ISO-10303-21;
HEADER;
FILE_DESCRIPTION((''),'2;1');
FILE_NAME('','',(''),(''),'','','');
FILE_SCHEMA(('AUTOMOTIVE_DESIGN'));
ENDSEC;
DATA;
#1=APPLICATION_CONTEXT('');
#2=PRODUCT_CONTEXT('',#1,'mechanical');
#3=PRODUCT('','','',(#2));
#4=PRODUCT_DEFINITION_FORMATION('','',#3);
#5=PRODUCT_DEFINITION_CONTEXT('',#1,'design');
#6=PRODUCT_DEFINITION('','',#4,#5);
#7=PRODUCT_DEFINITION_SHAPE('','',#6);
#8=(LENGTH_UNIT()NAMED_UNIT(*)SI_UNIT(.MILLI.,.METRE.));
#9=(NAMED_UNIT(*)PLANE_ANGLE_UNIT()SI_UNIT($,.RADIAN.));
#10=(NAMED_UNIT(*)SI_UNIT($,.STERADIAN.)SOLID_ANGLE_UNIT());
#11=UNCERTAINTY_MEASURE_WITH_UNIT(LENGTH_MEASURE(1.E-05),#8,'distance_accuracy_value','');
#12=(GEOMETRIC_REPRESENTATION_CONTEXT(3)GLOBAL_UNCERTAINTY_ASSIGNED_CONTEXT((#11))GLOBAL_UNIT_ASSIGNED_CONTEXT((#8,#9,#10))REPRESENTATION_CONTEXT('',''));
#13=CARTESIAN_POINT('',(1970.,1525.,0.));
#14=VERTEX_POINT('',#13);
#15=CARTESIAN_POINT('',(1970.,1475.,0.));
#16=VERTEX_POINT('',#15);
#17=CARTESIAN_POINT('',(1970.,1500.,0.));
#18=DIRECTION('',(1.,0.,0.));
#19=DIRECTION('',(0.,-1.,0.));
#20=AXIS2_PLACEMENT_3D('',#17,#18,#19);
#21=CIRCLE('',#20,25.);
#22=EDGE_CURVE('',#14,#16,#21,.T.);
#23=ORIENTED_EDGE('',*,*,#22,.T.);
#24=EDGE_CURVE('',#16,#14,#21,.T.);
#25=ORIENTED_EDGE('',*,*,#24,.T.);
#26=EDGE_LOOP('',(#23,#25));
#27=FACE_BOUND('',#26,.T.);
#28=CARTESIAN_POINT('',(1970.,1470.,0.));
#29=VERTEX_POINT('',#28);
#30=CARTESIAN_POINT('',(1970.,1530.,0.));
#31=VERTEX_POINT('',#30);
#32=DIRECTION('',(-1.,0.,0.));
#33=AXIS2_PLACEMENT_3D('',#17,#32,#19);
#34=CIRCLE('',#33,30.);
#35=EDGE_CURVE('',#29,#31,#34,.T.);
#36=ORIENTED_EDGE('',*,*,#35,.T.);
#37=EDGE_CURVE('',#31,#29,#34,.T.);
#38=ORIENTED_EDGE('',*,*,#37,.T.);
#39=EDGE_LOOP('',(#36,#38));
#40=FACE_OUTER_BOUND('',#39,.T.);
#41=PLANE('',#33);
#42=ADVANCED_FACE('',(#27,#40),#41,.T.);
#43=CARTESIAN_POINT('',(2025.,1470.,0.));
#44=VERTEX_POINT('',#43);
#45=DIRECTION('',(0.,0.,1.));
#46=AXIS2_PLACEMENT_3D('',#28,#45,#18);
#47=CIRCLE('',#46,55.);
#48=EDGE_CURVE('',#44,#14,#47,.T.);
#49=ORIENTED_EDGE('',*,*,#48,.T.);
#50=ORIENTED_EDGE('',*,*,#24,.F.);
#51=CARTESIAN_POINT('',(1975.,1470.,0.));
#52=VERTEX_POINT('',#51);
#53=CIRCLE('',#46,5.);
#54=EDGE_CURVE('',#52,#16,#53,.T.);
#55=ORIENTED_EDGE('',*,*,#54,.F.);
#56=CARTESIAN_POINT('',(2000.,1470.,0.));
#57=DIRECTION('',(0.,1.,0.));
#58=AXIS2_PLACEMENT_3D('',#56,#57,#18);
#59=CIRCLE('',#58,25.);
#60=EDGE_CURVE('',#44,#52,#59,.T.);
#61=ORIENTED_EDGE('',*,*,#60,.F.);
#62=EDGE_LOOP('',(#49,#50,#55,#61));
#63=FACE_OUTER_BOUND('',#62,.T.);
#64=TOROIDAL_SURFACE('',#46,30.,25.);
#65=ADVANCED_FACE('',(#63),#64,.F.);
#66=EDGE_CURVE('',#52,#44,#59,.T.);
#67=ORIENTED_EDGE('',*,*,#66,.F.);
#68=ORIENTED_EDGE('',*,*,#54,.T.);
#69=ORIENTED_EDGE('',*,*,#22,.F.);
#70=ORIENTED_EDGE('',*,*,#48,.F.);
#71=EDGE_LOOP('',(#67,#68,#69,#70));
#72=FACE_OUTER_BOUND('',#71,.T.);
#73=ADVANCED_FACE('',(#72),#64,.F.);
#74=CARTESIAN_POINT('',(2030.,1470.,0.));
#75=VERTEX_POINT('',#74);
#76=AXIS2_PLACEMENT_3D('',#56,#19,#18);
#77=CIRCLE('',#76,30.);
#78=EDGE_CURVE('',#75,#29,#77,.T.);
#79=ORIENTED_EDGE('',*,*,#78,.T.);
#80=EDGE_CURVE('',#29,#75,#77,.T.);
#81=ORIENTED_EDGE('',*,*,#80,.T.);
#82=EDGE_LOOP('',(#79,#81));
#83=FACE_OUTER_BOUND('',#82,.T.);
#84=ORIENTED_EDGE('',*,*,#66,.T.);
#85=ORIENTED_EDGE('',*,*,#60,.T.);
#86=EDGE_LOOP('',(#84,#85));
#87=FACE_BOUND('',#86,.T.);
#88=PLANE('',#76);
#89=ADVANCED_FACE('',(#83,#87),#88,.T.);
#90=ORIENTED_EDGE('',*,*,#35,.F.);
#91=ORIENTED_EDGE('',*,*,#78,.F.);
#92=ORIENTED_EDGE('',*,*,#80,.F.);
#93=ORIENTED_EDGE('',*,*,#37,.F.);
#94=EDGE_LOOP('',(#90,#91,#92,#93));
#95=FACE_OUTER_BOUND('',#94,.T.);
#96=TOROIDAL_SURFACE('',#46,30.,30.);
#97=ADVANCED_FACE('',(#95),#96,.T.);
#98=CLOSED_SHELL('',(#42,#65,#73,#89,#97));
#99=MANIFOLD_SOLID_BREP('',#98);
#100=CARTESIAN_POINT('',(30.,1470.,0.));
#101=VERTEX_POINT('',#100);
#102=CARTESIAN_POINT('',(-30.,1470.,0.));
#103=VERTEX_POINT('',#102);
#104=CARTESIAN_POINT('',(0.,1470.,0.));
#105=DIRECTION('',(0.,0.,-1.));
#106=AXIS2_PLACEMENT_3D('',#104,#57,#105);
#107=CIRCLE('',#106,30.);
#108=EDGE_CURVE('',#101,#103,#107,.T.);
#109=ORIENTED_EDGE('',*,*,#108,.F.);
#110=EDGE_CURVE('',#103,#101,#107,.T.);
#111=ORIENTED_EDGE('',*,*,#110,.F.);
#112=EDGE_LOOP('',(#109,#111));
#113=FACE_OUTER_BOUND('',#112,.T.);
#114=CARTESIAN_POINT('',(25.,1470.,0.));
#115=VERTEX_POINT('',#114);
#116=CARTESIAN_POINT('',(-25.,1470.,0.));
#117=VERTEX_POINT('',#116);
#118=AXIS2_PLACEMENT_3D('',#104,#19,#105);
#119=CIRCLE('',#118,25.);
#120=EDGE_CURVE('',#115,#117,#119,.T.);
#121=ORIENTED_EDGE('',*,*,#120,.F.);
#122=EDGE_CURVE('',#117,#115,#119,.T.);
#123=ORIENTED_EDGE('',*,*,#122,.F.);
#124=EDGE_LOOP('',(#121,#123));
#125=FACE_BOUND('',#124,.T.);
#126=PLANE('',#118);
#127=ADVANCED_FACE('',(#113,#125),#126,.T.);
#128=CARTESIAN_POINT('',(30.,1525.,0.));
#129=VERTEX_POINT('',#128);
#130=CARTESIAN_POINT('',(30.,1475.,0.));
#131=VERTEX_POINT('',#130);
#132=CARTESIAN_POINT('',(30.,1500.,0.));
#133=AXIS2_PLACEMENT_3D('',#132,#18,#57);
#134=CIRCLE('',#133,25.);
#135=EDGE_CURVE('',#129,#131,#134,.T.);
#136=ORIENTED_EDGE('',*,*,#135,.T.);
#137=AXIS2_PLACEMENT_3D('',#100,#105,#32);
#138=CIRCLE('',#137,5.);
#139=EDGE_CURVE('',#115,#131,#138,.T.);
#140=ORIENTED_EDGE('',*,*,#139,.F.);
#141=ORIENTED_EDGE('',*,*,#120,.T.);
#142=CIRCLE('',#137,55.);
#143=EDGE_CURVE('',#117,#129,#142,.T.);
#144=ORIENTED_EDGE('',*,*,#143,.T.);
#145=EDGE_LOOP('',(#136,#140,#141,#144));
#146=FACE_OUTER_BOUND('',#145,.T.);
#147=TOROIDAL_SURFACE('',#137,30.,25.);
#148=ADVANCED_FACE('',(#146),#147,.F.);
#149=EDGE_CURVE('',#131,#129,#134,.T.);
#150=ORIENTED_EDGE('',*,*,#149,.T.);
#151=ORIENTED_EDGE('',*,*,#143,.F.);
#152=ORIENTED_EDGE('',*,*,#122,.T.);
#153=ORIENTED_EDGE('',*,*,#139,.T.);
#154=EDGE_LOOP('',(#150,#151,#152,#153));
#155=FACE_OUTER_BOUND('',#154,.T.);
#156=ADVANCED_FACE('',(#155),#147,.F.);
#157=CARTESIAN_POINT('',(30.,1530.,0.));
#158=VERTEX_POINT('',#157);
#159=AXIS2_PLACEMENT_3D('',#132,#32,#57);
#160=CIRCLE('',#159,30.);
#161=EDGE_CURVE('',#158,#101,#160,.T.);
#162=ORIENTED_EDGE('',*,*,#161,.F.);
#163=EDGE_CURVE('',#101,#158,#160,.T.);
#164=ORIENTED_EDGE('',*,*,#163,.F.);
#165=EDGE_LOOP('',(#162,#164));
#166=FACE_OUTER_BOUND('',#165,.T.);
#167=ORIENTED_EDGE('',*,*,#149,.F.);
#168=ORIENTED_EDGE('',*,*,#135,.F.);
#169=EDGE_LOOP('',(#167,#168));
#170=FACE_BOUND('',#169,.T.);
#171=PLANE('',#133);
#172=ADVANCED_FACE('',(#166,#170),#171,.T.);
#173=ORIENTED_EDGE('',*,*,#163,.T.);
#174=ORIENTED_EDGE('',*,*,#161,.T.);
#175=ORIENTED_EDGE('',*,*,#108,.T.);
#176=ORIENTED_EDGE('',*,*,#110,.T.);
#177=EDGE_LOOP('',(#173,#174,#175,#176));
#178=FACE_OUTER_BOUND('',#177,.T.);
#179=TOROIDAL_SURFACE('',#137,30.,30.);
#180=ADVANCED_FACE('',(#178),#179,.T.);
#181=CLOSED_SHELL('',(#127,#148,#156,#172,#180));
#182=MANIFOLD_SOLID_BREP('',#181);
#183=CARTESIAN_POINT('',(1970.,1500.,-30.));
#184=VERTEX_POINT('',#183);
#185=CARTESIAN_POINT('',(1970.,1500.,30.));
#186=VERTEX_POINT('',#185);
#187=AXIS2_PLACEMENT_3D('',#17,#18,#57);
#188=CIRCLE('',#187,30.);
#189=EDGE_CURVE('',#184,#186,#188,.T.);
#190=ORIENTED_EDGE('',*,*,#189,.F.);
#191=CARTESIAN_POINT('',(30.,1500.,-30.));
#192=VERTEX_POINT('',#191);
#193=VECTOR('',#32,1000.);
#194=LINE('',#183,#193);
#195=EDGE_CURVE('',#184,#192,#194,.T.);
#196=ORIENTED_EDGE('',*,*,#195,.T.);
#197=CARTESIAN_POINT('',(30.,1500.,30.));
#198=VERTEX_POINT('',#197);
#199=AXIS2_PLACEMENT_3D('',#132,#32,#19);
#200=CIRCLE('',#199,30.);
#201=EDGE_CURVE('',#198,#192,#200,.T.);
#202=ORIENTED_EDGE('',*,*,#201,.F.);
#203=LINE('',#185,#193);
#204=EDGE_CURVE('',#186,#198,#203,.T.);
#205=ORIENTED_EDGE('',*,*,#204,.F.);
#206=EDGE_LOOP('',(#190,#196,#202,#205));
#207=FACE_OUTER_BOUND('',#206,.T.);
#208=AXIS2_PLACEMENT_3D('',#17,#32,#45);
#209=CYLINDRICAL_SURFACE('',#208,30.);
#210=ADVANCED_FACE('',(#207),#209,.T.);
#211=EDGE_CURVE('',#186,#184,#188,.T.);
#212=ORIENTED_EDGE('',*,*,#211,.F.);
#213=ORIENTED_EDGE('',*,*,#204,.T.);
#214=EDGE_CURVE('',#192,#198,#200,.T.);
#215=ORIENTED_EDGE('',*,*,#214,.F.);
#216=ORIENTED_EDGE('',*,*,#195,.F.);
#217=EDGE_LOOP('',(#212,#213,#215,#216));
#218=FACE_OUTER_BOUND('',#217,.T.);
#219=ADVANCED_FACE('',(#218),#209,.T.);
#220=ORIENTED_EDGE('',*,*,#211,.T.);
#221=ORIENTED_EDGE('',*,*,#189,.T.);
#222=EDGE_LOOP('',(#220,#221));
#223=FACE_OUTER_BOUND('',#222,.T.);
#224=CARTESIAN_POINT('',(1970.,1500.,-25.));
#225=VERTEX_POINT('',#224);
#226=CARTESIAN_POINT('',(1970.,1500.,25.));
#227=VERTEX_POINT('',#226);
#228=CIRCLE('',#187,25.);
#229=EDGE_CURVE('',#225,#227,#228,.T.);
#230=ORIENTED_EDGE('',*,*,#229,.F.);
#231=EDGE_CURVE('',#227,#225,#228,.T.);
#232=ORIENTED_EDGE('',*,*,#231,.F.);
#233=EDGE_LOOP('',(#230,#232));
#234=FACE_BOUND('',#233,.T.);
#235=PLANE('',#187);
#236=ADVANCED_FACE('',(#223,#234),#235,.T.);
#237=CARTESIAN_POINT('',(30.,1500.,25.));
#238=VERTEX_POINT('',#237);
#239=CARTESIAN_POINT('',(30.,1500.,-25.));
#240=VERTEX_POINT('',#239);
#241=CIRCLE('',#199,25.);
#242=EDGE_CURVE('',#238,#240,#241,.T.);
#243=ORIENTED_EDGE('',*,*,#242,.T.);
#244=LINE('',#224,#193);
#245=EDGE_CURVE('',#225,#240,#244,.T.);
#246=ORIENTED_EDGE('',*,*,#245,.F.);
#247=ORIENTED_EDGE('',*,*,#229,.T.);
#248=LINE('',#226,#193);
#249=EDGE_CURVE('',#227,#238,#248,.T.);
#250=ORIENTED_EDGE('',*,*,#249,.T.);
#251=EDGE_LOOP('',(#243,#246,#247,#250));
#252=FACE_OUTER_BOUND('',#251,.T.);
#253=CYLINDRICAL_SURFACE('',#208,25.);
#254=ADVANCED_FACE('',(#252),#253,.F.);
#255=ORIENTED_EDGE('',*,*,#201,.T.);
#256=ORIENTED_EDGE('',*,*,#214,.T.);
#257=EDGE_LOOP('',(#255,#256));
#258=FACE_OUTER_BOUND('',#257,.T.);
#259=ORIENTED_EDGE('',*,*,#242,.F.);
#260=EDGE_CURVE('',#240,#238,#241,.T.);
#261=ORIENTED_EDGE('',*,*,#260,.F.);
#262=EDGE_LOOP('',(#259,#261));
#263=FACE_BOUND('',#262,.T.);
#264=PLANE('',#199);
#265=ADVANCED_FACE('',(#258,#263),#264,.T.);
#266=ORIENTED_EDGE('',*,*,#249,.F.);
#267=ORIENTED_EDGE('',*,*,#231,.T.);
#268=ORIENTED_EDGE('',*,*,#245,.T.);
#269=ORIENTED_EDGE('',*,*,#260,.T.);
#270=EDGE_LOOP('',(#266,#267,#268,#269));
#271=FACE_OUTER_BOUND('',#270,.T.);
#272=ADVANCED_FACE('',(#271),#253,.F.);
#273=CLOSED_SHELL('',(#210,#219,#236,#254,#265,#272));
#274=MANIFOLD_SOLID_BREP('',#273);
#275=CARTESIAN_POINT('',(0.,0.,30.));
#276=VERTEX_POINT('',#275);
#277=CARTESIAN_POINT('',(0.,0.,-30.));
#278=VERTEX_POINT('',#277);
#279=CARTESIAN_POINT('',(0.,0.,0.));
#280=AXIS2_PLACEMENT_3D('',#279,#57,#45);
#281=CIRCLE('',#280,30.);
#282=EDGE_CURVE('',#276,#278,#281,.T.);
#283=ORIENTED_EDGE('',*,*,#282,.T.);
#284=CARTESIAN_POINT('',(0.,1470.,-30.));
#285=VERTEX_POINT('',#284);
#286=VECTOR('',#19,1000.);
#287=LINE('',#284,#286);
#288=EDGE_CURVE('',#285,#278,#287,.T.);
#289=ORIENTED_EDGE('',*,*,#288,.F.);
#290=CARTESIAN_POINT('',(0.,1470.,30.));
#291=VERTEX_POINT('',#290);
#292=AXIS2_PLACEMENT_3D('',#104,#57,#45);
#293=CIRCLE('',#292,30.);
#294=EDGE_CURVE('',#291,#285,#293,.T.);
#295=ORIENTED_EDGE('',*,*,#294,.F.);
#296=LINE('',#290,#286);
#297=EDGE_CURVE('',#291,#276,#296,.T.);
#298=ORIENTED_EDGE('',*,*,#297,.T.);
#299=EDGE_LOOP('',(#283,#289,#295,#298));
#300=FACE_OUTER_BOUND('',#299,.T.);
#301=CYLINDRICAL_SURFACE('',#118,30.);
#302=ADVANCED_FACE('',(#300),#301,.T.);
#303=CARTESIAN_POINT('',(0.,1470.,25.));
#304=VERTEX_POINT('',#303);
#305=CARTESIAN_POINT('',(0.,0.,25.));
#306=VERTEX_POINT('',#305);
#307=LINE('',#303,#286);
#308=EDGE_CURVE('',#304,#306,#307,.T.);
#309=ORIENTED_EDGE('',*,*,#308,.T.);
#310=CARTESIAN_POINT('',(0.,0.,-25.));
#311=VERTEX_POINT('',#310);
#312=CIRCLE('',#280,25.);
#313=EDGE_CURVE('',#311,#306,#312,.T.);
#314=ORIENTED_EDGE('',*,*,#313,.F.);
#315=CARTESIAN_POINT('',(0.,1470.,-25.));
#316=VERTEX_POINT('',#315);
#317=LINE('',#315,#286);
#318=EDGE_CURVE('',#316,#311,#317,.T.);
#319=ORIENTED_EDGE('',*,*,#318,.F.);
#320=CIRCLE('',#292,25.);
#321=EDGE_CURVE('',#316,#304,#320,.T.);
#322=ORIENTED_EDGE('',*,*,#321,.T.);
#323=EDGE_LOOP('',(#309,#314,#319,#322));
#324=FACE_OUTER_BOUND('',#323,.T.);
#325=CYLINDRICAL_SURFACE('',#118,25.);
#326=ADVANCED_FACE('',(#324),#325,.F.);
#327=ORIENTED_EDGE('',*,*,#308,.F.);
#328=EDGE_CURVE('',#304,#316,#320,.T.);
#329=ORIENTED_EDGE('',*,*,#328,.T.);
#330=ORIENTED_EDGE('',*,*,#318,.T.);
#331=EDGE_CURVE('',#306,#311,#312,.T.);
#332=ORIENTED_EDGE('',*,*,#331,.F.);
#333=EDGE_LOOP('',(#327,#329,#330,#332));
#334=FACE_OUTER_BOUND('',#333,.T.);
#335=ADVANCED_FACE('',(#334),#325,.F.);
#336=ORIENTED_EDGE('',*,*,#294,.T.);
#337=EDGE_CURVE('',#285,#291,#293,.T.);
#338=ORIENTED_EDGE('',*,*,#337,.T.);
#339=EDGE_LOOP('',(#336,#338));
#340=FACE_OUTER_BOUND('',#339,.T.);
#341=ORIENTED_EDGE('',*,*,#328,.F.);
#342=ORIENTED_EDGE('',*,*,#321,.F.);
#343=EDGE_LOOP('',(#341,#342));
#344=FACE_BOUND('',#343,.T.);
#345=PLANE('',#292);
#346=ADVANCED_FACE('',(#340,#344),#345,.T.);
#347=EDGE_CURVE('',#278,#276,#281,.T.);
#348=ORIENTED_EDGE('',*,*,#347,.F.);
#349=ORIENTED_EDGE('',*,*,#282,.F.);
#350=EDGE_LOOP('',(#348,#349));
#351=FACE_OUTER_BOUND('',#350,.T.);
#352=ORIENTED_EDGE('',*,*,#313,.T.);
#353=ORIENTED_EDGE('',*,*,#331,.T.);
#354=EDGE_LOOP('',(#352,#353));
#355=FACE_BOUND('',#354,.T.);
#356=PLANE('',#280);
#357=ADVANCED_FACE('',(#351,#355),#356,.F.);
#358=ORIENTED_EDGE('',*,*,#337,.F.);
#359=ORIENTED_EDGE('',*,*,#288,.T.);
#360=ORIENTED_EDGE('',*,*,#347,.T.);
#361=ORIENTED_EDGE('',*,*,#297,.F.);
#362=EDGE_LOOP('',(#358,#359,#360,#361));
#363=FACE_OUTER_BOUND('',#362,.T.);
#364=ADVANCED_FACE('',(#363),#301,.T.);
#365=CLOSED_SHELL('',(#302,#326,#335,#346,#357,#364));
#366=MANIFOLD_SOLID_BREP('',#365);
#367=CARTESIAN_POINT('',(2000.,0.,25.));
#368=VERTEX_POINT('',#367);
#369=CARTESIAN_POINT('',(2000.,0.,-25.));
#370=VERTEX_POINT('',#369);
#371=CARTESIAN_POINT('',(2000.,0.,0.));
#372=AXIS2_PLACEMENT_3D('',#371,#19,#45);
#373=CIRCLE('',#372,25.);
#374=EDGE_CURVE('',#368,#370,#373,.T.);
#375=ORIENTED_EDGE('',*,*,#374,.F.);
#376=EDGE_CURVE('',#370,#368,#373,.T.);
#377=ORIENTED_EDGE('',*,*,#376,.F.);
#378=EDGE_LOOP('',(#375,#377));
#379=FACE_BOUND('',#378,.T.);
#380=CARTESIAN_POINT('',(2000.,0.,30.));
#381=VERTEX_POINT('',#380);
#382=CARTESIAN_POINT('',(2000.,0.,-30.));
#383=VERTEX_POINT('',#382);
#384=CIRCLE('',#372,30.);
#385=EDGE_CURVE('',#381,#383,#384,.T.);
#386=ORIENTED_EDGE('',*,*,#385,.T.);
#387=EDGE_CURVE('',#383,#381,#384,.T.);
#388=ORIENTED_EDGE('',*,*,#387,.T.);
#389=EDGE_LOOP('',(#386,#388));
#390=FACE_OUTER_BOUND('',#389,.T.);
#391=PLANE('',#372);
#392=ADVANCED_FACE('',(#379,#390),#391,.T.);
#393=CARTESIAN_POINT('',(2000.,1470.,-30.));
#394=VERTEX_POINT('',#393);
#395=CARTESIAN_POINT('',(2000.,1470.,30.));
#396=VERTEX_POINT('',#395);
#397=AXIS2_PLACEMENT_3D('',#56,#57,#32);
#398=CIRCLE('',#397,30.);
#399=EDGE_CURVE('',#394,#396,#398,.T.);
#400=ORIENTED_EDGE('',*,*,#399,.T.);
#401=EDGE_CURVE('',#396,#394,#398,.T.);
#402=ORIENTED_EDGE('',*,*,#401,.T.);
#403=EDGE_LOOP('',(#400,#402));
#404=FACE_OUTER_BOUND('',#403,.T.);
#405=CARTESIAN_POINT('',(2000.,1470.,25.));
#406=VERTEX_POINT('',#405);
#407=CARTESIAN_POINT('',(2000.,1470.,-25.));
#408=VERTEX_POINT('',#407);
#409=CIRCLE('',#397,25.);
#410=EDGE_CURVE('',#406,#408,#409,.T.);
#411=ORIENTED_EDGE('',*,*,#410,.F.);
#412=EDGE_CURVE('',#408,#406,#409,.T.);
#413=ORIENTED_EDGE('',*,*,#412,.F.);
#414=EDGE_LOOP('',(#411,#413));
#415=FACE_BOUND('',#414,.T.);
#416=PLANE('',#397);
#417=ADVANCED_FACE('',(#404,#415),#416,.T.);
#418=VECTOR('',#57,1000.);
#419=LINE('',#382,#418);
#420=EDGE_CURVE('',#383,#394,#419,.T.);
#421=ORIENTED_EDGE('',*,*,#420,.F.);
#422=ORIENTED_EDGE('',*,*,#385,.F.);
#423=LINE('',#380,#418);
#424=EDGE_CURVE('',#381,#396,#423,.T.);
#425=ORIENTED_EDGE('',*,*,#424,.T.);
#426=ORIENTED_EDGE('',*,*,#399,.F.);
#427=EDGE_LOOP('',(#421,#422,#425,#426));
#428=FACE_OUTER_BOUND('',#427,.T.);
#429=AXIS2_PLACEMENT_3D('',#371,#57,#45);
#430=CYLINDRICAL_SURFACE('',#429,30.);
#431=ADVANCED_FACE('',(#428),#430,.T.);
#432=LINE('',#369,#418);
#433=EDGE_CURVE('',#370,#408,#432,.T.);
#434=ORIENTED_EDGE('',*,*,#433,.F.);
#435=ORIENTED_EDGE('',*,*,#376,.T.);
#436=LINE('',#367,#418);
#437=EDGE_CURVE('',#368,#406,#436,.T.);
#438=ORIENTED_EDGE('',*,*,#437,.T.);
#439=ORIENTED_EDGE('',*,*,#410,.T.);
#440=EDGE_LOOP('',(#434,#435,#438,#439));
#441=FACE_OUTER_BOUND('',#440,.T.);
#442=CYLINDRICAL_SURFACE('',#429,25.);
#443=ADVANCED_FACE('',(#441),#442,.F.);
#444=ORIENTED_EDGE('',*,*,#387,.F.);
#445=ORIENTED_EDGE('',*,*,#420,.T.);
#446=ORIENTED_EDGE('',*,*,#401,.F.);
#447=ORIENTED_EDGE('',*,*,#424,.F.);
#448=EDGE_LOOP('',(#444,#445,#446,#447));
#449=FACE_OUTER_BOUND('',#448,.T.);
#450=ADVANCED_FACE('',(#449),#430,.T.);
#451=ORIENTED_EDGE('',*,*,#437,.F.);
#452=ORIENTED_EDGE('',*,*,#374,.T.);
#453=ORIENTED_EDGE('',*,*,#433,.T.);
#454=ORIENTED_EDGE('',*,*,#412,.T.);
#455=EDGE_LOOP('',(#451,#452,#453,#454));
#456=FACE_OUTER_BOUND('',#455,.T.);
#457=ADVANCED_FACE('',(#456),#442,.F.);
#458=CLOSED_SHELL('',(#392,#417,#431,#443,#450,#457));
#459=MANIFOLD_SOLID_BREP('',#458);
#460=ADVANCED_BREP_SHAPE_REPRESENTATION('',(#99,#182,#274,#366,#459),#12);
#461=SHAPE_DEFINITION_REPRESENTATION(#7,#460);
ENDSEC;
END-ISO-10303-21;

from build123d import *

# Parameters (mm, degrees)
SKETCH1_R                                  = 30
SKETCH1_R_2                                = 25
GB_T6728_2002_ROUND_TUBE_060_X_5_1_DEPTH   = 1470
SKETCH1_ON_SEGMENT_2_R                     = 30
SKETCH1_ON_SEGMENT_2_R_2                   = 25
GB_T6728_2002_ROUND_TUBE_060_X_5_1_2_ANGLE = 90
SKETCH1_ON_SEGMENT_3_R                     = 30
SKETCH1_ON_SEGMENT_3_R_2                   = 25
GB_T6728_2002_ROUND_TUBE_060_X_5_1_3_DEPTH = 1940
SKETCH1_ON_SEGMENT_4_R                     = 30
SKETCH1_ON_SEGMENT_4_R_2                   = 25
GB_T6728_2002_ROUND_TUBE_060_X_5_1_4_ANGLE = 90
SKETCH1_ON_SEGMENT_5_R                     = 30
SKETCH1_ON_SEGMENT_5_R_2                   = 25
GB_T6728_2002_ROUND_TUBE_060_X_5_1_5_DEPTH = 1470


with BuildPart() as part:
    # Sketch1 → Gb／t6728-2002 round tube 060 X 5 (1) (new body)
    with BuildSketch(Plane(origin=(0, 0, 0), x_dir=(1, 0, 0), z_dir=(0, 1, 0))):
        Circle(SKETCH1_R)
        Circle(SKETCH1_R_2, mode=Mode.SUBTRACT)
    extrude(amount=GB_T6728_2002_ROUND_TUBE_060_X_5_1_DEPTH)


with BuildPart() as body_2:
    # Sketch1 on segment 2 (carried to the start of arc 2) → Gb_t6728-2002 round tube 060 X 5 _1 2 (revolve)
    with BuildSketch(Plane(origin=(0, 1470, 0), x_dir=(1, 0, 0), z_dir=(0, 1, 0))):
        Circle(SKETCH1_ON_SEGMENT_2_R)
        Circle(SKETCH1_ON_SEGMENT_2_R_2, mode=Mode.SUBTRACT)
    revolve(axis=Axis((30, 1470, 0), (0, 0, -1)), revolution_arc=GB_T6728_2002_ROUND_TUBE_060_X_5_1_2_ANGLE)


with BuildPart() as body_3:
    # Sketch1 on segment 3 (carried to segment 3) → Gb_t6728-2002 round tube 060 X 5 _1 3 (new body)
    with BuildSketch(Plane(origin=(30, 1500, 0), x_dir=(0, -1, 0), z_dir=(1, 0, 0))):
        Circle(SKETCH1_ON_SEGMENT_3_R)
        Circle(SKETCH1_ON_SEGMENT_3_R_2, mode=Mode.SUBTRACT)
    extrude(amount=GB_T6728_2002_ROUND_TUBE_060_X_5_1_3_DEPTH)


with BuildPart() as body_4:
    # Sketch1 on segment 4 (carried to the start of arc 4) → Gb_t6728-2002 round tube 060 X 5 _1 4 (revolve)
    with BuildSketch(Plane(origin=(2000, 1470, 0), x_dir=(1, 0, 0), z_dir=(0, 1, 0))):
        Circle(SKETCH1_ON_SEGMENT_4_R)
        Circle(SKETCH1_ON_SEGMENT_4_R_2, mode=Mode.SUBTRACT)
    revolve(axis=Axis((1970, 1470, 0), (0, 0, 1)), revolution_arc=GB_T6728_2002_ROUND_TUBE_060_X_5_1_4_ANGLE)


with BuildPart() as body_5:
    # Sketch1 on segment 5 (carried to segment 5) → Gb_t6728-2002 round tube 060 X 5 _1 5 (new body)
    with BuildSketch(Plane(origin=(2000, 0, 0), x_dir=(1, 0, 0), z_dir=(0, 1, 0))):
        Circle(SKETCH1_ON_SEGMENT_5_R)
        Circle(SKETCH1_ON_SEGMENT_5_R_2, mode=Mode.SUBTRACT)
    extrude(amount=GB_T6728_2002_ROUND_TUBE_060_X_5_1_5_DEPTH)


solid = Compound([part.part, body_2.part, body_3.part, body_4.part, body_5.part])
